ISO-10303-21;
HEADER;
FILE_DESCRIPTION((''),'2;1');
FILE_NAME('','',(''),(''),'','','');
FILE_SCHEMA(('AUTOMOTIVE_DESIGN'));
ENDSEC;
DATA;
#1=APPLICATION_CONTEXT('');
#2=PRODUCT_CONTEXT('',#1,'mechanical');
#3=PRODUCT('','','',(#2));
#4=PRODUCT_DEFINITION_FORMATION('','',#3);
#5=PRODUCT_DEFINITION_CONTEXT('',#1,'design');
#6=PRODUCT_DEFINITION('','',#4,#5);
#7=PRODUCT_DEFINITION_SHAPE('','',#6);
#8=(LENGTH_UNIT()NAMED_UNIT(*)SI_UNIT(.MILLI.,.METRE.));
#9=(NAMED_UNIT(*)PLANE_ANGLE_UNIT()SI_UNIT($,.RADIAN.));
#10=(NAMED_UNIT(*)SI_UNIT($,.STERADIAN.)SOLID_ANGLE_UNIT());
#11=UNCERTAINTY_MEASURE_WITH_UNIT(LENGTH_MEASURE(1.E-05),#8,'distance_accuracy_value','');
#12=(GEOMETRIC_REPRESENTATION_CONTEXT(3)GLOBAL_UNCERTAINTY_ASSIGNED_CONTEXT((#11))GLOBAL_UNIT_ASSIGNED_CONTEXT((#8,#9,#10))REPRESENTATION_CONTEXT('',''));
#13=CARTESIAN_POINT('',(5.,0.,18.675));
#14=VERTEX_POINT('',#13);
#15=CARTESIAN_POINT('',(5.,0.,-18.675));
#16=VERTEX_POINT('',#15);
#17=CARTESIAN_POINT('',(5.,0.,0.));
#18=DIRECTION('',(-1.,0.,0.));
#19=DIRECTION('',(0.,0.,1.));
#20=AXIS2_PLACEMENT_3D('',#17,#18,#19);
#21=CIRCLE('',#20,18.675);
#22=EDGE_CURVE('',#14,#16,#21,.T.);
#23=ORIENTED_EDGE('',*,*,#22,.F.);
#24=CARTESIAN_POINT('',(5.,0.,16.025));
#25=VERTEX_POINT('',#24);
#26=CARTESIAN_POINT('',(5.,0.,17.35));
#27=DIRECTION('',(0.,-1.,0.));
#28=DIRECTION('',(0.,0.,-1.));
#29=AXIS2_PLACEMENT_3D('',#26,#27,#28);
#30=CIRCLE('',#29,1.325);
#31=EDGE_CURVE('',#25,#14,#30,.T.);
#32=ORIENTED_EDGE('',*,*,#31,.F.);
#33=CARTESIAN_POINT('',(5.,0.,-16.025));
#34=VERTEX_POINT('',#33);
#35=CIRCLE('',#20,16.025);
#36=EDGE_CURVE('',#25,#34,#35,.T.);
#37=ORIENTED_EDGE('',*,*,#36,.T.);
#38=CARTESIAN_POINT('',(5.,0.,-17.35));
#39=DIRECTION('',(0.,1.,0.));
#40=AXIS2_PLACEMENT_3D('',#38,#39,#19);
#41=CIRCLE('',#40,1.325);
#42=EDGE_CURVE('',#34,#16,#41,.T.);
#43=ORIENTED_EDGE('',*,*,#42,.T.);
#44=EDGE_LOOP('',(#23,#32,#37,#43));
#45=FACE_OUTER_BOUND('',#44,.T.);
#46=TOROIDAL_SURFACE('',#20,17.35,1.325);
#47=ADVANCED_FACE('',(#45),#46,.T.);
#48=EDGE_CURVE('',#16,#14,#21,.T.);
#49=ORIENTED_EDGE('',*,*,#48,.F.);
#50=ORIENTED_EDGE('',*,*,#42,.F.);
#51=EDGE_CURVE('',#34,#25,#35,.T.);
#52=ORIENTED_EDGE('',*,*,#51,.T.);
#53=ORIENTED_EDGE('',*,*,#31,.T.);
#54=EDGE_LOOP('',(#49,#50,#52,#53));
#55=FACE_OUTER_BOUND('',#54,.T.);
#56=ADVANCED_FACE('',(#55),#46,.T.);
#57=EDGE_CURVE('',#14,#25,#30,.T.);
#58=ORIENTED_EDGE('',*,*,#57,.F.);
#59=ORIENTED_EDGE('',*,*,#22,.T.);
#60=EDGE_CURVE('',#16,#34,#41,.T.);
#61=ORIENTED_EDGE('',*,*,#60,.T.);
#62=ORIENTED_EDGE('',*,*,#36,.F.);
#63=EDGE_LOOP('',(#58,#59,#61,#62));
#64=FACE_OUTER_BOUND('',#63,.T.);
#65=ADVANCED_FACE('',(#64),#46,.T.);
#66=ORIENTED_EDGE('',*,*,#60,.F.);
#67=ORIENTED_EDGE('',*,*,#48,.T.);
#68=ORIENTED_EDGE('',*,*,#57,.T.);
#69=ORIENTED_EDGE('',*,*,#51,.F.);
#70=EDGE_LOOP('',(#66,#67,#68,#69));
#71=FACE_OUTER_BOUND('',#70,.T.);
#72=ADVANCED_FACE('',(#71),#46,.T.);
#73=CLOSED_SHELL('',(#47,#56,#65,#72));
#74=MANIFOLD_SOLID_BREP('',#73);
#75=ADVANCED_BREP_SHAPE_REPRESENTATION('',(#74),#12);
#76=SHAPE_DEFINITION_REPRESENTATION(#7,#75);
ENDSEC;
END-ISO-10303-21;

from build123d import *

# Parameters (mm, degrees)
SKETCH1_R = 1.325


with BuildPart() as part:
    # Sketch1 → Revolve1 (revolve)
    with BuildSketch(Plane.XY, mode=Mode.PRIVATE) as revolve1_sk:
        with Locations((5, 17.35)):
            Circle(SKETCH1_R)
    revolve(revolve1_sk.sketch.rotate(Axis((0, 0, 0), (1, 0, 0)), 90), axis=Axis((0, 0, 0), (1, 0, 0)))


solid = part.part
